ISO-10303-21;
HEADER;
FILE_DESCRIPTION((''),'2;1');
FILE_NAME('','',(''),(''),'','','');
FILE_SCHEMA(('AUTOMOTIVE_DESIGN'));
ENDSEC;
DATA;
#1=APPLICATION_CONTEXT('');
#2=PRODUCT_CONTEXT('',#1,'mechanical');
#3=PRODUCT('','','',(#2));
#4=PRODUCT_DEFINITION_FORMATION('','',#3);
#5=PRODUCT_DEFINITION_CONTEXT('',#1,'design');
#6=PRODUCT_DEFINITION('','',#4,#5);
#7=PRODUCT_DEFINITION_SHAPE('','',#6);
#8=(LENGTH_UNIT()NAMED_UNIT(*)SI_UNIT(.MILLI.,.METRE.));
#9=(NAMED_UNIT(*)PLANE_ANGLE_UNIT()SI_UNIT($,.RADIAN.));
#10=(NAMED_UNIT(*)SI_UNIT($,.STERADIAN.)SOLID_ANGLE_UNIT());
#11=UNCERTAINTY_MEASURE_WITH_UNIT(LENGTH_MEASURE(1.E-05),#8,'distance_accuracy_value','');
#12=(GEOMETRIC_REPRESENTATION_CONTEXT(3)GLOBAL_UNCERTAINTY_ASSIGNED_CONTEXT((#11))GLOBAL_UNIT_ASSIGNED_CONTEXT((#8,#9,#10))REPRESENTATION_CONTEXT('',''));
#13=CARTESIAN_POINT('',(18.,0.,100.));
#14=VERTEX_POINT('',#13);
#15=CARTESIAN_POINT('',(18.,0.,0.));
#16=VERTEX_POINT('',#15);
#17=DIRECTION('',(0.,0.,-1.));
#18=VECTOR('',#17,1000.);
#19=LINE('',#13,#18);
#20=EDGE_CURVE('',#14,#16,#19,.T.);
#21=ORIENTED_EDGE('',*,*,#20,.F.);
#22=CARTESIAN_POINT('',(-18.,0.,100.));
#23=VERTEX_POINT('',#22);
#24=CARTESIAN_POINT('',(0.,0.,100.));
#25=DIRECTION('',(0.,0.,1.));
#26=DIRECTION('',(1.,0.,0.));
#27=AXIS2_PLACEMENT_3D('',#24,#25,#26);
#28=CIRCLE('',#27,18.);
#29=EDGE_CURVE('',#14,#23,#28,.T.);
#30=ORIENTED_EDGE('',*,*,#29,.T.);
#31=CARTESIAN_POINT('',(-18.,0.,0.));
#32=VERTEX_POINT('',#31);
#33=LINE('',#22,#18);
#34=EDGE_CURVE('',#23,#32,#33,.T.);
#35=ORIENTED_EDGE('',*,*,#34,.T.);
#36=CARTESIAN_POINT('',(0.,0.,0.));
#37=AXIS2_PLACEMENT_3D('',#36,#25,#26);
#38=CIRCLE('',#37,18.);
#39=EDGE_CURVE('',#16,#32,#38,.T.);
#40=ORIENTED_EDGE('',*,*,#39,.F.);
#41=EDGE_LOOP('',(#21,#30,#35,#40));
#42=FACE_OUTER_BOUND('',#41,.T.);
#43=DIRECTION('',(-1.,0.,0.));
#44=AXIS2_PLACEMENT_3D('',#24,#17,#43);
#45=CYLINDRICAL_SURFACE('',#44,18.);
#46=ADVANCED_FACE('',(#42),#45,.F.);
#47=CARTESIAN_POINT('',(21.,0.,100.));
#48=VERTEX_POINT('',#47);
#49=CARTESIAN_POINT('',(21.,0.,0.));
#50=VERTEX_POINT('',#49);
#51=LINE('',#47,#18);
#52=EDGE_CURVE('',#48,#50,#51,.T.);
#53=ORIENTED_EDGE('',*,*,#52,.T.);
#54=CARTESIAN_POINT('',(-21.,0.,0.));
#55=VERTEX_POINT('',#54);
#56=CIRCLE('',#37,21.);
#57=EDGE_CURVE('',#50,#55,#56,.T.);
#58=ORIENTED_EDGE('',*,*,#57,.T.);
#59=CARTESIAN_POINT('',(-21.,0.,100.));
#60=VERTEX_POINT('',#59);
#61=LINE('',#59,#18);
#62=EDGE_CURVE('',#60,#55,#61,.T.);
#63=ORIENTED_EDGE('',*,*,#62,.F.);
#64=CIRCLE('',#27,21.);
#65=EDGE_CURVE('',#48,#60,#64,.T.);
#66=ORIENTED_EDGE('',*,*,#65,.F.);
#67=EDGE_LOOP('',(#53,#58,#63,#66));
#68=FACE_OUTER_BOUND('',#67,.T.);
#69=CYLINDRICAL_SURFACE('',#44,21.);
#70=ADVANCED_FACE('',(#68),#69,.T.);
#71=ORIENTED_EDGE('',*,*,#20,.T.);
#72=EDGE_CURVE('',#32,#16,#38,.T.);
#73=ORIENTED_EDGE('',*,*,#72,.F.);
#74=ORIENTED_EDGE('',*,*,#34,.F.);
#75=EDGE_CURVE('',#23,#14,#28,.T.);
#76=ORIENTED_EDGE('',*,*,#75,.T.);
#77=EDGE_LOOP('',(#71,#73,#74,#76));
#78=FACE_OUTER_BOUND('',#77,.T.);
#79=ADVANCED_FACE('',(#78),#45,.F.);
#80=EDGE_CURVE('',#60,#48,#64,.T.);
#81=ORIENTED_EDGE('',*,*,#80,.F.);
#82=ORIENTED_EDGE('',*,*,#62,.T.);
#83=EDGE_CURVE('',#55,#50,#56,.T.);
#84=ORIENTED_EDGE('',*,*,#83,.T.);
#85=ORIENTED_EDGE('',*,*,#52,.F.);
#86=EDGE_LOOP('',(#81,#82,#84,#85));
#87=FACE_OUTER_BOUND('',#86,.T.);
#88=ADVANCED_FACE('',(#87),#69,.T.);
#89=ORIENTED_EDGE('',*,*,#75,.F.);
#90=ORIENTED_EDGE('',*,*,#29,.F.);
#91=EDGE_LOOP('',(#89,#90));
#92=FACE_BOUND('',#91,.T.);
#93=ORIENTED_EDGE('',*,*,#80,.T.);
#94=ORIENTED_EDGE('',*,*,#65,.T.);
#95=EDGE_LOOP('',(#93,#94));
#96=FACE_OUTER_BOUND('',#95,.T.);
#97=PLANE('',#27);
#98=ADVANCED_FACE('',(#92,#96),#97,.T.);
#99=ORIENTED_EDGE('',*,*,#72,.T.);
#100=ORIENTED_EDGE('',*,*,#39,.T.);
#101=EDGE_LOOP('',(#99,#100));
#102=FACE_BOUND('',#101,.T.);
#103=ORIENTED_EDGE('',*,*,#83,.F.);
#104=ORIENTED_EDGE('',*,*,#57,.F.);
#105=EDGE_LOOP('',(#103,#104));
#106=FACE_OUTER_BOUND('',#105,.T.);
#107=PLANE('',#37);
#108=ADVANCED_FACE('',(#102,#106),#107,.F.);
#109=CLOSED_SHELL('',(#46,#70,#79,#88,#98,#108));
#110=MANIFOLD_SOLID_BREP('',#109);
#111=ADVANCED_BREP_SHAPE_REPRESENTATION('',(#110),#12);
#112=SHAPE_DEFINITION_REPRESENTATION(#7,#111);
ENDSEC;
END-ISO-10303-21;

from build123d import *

# Parameters (mm, degrees)
SKETCH_1_R           = 21
SKETCH_1_R_2         = 18
BOSS_EXTRUDE_1_DEPTH = 100


with BuildPart() as part:
    # Sketch 1 → Boss-Extrude 1 (new body)
    with BuildSketch(Plane.XY):
        Circle(SKETCH_1_R)
        Circle(SKETCH_1_R_2, mode=Mode.SUBTRACT)
    extrude(amount=BOSS_EXTRUDE_1_DEPTH)


solid = part.part
